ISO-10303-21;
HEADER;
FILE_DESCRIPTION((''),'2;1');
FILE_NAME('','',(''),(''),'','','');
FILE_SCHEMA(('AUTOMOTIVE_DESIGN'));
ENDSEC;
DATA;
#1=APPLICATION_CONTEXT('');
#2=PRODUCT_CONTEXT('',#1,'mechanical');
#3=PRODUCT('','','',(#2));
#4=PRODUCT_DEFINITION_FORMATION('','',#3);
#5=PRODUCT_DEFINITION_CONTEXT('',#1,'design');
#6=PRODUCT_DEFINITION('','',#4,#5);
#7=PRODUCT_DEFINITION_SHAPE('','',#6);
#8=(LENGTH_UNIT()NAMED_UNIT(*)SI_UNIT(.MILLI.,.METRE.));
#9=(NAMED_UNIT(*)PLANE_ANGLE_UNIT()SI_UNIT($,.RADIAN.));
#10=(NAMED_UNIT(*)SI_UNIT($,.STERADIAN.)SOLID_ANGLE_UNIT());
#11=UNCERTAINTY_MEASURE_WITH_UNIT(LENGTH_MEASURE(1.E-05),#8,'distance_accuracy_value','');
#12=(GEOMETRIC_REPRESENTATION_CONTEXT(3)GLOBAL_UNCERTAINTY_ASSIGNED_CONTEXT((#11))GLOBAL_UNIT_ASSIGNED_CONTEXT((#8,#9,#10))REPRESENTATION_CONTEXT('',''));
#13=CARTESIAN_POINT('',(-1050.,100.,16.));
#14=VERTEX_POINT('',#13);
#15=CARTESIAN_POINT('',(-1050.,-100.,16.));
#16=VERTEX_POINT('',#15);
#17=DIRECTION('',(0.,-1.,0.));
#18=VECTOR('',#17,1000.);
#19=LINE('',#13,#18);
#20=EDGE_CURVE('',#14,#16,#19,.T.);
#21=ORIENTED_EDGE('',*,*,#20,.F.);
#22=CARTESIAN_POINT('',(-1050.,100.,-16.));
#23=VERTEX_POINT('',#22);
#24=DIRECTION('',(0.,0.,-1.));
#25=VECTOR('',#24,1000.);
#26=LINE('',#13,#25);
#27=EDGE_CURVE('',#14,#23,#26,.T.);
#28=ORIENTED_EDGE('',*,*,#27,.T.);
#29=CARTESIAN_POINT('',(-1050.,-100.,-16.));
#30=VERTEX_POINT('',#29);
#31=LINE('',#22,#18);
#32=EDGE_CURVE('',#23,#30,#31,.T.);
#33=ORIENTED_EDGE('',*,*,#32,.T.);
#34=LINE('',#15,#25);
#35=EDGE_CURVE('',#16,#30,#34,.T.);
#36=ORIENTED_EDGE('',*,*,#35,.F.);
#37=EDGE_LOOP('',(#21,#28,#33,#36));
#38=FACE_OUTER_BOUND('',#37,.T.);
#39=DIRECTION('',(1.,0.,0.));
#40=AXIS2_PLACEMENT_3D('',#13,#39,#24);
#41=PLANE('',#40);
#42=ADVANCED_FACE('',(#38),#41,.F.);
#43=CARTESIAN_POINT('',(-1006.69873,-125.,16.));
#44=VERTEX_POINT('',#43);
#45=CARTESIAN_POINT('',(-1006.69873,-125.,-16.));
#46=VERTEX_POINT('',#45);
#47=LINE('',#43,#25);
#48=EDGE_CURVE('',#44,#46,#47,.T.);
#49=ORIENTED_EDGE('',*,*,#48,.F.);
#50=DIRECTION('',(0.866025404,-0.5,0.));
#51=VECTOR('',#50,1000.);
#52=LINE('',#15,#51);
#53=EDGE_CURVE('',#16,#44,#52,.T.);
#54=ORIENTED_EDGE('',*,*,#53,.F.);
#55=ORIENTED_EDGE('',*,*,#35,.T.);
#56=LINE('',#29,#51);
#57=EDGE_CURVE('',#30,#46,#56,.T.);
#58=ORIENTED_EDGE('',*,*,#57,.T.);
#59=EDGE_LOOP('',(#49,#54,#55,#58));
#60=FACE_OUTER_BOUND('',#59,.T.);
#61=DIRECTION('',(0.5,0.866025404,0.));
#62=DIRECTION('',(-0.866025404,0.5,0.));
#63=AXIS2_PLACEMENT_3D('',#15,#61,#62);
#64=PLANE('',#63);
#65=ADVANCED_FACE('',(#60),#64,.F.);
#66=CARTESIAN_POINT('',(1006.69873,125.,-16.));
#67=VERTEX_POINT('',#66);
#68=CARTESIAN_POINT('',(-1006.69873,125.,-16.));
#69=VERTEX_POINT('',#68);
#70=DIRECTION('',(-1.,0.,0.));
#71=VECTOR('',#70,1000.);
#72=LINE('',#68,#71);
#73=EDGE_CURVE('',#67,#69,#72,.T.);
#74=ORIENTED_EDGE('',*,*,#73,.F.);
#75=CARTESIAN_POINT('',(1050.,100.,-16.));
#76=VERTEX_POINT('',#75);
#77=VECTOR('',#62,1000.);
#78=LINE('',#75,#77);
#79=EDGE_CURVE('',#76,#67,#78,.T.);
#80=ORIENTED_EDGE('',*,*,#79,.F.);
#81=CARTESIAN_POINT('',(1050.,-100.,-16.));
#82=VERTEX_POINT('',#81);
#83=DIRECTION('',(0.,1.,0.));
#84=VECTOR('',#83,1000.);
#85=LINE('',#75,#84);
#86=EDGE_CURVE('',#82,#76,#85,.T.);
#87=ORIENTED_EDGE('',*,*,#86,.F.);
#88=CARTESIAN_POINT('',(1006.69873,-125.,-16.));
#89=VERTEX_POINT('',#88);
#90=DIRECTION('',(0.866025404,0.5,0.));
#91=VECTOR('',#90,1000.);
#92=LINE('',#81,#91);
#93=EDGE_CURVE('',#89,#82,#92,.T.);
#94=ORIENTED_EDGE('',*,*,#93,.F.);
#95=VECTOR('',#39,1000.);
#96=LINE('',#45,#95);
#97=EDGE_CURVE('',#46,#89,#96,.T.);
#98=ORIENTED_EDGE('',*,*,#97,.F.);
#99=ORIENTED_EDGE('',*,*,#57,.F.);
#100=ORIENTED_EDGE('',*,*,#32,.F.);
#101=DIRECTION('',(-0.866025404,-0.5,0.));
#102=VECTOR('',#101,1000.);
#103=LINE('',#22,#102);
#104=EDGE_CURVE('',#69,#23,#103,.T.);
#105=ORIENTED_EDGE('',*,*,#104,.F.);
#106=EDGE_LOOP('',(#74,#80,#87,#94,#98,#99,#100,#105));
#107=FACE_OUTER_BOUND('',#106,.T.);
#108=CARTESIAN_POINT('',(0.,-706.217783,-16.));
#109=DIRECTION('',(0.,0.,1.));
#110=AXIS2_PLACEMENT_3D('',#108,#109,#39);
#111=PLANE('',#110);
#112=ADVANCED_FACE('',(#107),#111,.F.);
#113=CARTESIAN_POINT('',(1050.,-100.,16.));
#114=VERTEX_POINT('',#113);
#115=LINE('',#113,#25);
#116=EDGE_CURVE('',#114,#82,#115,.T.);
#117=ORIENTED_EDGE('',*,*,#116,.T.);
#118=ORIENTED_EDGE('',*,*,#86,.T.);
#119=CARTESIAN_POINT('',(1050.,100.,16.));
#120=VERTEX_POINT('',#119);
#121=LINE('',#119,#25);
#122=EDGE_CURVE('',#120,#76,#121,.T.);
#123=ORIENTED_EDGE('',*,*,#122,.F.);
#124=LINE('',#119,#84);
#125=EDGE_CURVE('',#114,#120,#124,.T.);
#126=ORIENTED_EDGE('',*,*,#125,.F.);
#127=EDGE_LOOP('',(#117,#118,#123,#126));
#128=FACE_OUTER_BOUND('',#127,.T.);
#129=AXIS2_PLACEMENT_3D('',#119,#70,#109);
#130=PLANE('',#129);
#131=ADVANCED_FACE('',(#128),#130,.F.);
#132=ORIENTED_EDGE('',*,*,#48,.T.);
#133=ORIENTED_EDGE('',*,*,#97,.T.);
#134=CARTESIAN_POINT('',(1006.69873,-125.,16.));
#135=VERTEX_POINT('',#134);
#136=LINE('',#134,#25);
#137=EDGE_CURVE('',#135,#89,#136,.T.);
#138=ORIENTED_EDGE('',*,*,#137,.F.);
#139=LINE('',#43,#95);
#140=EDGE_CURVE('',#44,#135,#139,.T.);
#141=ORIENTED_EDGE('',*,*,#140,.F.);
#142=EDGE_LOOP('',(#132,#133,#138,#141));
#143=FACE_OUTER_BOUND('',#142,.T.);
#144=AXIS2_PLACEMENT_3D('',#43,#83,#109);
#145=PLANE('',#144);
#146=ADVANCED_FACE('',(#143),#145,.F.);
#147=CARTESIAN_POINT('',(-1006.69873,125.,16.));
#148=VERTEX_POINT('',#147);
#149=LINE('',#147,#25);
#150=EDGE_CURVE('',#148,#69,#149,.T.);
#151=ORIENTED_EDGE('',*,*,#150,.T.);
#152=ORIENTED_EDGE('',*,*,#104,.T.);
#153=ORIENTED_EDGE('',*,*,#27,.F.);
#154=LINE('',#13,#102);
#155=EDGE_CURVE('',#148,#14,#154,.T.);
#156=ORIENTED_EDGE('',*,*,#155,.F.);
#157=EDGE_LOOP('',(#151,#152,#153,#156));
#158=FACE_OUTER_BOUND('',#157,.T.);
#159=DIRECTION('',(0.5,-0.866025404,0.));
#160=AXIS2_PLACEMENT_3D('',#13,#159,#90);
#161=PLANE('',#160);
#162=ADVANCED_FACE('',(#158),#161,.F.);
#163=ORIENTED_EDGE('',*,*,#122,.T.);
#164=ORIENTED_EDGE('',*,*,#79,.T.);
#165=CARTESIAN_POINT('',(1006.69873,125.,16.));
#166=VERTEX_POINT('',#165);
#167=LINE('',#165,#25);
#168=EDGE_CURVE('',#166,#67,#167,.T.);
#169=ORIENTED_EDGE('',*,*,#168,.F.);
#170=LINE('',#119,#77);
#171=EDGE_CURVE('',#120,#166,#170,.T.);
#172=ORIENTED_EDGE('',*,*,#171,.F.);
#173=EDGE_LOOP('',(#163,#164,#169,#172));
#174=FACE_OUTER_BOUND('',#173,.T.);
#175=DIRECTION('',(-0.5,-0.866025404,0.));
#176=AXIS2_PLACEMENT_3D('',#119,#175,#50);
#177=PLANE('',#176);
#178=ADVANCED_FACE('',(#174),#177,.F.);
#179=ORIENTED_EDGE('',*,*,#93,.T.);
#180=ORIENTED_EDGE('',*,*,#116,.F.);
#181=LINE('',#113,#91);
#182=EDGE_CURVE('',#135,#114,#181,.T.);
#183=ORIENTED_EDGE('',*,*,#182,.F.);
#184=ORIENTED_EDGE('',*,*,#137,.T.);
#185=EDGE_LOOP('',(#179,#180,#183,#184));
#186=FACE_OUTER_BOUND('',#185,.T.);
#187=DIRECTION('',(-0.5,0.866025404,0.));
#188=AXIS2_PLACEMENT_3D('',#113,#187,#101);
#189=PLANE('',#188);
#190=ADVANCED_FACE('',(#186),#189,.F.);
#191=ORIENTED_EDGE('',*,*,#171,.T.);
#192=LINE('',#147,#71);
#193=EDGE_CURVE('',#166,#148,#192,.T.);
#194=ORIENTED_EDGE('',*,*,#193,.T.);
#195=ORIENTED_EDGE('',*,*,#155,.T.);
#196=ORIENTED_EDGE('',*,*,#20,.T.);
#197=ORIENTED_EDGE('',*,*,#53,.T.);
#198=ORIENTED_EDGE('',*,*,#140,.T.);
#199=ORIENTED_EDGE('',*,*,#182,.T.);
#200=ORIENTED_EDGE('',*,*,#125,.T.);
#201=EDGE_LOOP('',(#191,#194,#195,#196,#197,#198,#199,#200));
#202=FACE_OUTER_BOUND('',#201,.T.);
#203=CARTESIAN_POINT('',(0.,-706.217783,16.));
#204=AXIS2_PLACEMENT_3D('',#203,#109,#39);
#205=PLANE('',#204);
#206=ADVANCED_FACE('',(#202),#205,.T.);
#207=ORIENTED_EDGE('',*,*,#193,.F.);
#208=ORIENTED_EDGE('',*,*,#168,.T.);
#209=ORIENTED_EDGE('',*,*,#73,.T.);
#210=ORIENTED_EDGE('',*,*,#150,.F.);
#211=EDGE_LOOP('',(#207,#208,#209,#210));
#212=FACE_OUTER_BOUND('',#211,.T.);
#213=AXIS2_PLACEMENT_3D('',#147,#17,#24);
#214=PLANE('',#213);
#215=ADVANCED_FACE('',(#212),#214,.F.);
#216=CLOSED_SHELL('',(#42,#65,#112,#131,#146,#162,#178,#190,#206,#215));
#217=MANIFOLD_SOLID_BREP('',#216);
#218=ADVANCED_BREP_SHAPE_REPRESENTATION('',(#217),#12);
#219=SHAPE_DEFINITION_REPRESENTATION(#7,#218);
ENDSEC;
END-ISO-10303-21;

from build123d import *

# Parameters (mm, degrees)
BOSS_EXTRUDE1_DEPTH = 16


with BuildPart() as part:
    # Sketch1 → Boss-Extrude1 (new, symmetric)
    with BuildSketch(Plane.XY):
        Polygon((1050, 100), (1006.698729811, 125), (-1006.698729811, 125), (-1050, 100), (-1050, -100), (-1006.698729811, -125), (1006.698729811, -125), (1050, -100), align=None)
    extrude(amount=BOSS_EXTRUDE1_DEPTH, both=True)


solid = part.part
